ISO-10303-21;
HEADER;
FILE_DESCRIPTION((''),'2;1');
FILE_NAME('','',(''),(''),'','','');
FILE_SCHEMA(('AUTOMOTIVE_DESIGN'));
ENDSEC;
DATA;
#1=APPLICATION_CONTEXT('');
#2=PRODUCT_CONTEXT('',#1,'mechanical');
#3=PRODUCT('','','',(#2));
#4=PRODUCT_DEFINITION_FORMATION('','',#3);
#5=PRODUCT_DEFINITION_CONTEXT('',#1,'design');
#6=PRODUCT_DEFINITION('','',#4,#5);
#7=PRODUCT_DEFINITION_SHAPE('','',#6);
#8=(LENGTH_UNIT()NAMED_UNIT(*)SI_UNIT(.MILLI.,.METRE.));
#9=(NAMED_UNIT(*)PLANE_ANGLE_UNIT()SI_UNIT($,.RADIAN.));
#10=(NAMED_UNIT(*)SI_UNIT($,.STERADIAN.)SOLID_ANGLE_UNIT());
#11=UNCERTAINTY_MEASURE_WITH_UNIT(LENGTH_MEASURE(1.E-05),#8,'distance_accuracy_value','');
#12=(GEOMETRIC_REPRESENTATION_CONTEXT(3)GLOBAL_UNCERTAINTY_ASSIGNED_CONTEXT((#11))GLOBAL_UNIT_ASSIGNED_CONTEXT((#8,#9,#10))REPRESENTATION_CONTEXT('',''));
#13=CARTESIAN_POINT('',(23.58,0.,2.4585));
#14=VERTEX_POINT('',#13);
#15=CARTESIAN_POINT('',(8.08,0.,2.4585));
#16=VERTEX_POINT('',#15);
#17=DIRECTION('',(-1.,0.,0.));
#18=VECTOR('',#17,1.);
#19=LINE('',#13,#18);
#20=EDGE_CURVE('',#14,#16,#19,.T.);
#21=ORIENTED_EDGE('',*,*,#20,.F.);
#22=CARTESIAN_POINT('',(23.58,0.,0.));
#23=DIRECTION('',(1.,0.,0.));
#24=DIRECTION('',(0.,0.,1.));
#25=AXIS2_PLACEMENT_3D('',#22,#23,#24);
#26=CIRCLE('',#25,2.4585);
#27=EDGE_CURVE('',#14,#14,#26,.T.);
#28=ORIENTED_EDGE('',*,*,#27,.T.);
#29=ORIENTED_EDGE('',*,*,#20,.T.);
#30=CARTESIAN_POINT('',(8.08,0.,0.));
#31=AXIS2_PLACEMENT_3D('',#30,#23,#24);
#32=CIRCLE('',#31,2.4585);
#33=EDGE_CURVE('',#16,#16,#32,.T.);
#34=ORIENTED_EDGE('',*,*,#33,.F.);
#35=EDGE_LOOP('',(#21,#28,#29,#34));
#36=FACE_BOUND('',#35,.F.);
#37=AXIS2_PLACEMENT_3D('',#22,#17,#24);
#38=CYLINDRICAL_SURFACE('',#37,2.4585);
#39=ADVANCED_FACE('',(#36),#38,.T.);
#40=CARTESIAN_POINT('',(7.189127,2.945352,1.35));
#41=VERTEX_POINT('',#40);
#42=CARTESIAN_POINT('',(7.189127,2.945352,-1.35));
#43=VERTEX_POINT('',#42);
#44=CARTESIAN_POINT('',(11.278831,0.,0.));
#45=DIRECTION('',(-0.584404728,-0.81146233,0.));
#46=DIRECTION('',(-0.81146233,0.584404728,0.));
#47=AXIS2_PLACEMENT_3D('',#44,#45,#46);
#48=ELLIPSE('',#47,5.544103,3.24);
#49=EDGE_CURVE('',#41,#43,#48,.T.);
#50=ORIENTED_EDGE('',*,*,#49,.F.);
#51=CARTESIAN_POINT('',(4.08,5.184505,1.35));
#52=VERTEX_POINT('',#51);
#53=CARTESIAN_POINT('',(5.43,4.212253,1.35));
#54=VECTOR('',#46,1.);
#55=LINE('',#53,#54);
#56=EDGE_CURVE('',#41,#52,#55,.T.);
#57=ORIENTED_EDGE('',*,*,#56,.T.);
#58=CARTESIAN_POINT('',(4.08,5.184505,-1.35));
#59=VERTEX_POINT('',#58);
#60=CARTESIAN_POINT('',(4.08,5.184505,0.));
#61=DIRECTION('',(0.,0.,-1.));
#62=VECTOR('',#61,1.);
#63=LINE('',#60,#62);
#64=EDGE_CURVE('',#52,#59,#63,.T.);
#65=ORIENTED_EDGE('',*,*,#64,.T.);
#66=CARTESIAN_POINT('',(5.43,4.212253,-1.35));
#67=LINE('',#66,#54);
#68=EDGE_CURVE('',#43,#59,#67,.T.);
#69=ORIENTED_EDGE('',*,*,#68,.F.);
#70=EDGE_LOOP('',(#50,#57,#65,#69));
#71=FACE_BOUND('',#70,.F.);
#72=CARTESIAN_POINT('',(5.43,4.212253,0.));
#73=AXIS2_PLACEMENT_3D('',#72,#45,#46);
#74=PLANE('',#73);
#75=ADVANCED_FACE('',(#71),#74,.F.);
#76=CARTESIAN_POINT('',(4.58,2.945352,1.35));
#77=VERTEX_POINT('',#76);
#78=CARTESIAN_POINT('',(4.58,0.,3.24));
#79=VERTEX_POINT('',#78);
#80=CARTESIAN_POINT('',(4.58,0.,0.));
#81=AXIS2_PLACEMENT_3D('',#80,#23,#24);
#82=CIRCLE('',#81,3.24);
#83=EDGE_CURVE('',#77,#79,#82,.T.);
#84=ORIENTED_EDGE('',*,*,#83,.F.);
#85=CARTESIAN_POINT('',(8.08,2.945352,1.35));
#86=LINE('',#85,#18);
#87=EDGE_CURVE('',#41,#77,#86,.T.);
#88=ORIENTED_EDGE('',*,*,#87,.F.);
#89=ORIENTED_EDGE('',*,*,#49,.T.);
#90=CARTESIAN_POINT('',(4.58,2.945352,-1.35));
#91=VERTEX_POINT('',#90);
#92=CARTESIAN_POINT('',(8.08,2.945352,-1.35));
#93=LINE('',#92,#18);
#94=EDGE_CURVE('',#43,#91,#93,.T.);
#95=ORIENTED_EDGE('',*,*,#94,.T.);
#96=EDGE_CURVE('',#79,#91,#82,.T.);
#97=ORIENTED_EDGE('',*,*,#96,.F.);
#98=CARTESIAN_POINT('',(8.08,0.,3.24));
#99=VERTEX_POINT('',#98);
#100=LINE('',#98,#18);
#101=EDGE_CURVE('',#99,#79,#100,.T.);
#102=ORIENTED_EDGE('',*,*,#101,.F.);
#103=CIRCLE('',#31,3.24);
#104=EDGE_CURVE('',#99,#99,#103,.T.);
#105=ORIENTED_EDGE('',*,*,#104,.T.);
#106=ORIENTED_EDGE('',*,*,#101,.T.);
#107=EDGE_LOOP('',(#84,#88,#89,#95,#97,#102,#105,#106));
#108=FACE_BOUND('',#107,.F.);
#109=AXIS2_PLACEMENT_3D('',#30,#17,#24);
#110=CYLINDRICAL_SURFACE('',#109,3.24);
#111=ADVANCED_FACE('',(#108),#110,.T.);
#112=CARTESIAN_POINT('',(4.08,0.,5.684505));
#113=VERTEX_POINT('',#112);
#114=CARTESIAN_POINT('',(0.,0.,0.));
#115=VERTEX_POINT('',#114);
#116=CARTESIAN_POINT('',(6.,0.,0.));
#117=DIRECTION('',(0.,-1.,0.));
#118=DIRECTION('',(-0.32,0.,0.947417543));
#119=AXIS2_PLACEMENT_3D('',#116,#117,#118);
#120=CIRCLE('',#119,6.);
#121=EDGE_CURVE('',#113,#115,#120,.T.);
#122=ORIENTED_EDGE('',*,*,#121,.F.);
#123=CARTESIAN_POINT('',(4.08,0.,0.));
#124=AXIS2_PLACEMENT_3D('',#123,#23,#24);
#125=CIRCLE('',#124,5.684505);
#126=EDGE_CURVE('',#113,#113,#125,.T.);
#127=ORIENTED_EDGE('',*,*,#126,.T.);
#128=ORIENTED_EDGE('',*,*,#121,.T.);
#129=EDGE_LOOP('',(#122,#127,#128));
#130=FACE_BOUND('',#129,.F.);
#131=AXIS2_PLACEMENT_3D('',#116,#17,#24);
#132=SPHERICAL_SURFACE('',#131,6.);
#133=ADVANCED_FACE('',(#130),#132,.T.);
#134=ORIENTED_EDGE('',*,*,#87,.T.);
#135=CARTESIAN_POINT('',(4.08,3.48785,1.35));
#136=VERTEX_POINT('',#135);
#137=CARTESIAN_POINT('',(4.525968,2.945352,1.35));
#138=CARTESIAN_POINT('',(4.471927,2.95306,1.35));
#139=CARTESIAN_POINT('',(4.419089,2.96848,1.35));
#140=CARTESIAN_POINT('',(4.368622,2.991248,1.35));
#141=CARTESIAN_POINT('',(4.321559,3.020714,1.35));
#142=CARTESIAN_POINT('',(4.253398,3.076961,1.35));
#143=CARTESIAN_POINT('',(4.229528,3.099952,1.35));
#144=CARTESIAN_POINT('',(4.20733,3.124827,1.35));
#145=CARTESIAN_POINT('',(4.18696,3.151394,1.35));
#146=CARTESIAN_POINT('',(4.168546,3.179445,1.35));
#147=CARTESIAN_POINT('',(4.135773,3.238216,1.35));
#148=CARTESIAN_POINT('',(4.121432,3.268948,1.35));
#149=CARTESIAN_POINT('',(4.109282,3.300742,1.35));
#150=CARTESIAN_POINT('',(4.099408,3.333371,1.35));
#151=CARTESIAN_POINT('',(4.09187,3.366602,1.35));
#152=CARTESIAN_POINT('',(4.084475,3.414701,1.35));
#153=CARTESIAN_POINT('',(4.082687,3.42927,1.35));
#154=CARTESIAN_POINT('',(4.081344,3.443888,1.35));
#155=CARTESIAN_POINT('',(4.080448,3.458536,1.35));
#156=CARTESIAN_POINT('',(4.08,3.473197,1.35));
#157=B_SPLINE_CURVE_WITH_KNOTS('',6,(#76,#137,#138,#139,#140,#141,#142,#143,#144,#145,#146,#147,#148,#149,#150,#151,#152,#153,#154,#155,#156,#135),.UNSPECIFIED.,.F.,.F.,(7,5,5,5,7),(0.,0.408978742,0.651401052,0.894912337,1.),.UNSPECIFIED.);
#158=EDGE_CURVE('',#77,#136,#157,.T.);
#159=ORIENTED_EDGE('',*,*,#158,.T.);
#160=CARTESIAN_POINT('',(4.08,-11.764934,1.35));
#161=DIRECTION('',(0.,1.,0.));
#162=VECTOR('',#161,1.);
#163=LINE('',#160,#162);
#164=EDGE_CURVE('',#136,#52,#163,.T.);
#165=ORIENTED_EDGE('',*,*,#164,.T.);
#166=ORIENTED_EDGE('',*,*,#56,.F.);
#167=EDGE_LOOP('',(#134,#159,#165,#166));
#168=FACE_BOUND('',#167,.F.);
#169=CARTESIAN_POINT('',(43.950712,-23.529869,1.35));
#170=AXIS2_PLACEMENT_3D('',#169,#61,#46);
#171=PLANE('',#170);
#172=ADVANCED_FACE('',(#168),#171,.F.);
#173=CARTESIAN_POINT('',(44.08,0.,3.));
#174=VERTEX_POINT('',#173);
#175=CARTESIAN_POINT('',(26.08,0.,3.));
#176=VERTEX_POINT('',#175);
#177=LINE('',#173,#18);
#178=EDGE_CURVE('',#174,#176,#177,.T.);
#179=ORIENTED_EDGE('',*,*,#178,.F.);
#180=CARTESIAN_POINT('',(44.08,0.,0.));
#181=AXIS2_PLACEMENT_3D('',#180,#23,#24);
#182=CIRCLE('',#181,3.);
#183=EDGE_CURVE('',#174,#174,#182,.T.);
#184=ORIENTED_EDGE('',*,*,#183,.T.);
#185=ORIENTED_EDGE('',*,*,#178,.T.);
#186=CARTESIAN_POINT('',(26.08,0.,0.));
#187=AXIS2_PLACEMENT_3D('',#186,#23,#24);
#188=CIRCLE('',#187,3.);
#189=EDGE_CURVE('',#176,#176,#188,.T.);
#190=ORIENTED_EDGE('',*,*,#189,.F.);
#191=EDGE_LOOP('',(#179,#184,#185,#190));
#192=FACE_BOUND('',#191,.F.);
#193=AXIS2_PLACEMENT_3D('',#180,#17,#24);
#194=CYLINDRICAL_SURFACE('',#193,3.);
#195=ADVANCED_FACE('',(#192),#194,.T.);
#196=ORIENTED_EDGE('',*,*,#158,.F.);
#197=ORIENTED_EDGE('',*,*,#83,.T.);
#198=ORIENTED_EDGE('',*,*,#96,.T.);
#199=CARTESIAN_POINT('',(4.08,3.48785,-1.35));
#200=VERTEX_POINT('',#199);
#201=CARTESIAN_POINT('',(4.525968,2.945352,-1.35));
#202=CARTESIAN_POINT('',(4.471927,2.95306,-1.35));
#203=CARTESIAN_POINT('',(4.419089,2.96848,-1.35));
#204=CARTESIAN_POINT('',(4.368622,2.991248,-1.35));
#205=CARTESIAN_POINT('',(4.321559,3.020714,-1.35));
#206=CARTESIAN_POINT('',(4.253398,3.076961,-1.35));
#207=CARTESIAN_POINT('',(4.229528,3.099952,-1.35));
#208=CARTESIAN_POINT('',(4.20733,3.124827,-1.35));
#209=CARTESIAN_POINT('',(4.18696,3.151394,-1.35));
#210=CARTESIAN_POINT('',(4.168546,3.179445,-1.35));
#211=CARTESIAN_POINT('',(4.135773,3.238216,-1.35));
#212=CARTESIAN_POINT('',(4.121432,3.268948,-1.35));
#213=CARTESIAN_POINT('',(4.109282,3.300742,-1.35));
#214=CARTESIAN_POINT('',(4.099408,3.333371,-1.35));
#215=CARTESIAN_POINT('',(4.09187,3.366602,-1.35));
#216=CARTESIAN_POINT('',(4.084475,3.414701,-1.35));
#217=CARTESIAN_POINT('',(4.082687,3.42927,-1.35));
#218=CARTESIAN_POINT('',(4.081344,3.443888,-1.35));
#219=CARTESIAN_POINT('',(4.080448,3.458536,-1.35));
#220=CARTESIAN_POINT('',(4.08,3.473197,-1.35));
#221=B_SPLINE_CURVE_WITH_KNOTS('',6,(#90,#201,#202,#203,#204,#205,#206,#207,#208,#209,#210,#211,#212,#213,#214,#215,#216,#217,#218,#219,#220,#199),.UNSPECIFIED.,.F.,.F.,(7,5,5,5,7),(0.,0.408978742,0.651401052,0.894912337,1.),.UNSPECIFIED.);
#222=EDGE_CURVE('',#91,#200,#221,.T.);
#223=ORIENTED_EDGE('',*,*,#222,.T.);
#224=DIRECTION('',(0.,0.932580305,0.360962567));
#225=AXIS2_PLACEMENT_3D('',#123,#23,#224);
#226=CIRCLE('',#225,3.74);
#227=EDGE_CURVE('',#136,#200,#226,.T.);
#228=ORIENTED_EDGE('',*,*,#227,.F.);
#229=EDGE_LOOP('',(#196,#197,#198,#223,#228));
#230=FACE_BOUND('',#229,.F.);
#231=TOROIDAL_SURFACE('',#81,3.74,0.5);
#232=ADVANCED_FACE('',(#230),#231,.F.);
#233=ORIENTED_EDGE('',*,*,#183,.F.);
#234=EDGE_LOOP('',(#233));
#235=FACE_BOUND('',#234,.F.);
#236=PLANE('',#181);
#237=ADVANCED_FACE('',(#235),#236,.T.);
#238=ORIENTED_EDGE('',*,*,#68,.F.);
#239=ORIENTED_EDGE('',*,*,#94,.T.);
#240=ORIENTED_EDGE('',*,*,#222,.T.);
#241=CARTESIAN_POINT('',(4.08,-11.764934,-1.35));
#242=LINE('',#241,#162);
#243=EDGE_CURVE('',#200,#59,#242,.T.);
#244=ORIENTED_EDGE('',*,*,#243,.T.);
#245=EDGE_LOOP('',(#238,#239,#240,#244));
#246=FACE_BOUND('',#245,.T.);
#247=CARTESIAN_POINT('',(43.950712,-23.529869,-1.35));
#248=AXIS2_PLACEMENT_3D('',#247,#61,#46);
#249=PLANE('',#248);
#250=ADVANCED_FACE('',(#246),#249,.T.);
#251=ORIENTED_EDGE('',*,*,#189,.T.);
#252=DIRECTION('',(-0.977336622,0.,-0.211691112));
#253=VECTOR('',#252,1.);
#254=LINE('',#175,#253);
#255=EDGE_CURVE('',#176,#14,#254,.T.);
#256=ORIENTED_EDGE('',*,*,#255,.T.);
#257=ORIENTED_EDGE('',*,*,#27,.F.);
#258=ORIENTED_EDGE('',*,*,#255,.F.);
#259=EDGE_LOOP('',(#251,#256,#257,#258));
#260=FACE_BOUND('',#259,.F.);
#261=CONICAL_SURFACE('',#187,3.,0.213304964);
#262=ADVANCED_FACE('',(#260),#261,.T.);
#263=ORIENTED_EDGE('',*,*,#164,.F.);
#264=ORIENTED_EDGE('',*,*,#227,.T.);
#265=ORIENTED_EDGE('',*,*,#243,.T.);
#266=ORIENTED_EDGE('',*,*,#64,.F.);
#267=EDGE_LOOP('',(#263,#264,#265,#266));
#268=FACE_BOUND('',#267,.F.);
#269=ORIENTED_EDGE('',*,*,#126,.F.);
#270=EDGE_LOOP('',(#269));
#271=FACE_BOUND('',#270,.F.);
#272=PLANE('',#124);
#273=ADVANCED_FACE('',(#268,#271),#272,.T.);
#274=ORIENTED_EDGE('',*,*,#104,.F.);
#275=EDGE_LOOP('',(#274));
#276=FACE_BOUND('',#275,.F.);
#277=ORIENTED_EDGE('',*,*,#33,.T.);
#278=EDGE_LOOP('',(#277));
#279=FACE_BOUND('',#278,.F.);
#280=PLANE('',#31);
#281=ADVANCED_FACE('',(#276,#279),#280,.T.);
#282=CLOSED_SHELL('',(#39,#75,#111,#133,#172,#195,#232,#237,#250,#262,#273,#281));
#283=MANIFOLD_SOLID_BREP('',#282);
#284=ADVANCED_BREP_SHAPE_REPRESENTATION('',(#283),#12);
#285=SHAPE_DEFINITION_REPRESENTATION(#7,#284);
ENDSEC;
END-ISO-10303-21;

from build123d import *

# Parameters (mm, degrees)
NIB_REACH      = 46.807
SKETCH2_WALL_W = 94.941468098
SKETCH2_WALL_H = 2.7


with BuildPart() as part:
    # Sketch1 → Base (revolve)
    with BuildSketch(Plane.XY, mode=Mode.PRIVATE) as base_sk:
        with BuildLine():
            Line((44.08, 0), (44.08, 3))
            Line((44.08, 3), (8.08, 3))
            Line((8.08, 3), (8.08, 3.24))
            Line((8.08, 3.24), (4.58, 3.24))
            ThreePointArc((4.58, 3.24), (4.226446609, 3.386446609), (4.08, 3.74))
            Line((4.08, 3.74), (4.08, 5.684505256))
            ThreePointArc((4.08, 5.684505256), (1.125576957, 3.498571137), (0, 0))
            Line((0, 0), (44.08, 0))
        make_face()
    revolve(base_sk.sketch.rotate(Axis((-31.484345479, 0, 0), (1, 0, 0)), 90), axis=Axis((-31.484345479, 0, 0), (1, 0, 0)))

    # Sketch2 wall → Nib (add, up to next)
    with BuildSketch(Plane(origin=(5.43, 4.212252628, 0), x_dir=(-0.811462330335, 0.58440472829, 0), z_dir=(-0.58440472829, -0.811462330335, 0)), mode=Mode.PRIVATE) as nib_sk1:
        Rectangle(SKETCH2_WALL_W, SKETCH2_WALL_H)
    nib_tool1 = extrude(nib_sk1.sketch, amount=NIB_REACH, mode=Mode.PRIVATE) - part.part
    add(nib_tool1.solids().sort_by_distance((5.43, 4.212252628, 0))[0])

    # Sketch3 → Cut-Revolve1 (revolve, cut)
    with BuildSketch(Plane.XY, mode=Mode.PRIVATE) as cut_revolve1_sk:
        Polygon((26.08, 3), (23.58, 2.4585), (8.08, 2.4585), (8.08, 3), align=None)
    revolve(cut_revolve1_sk.sketch.rotate(Axis((-29.816341648, 0, 0), (1, 0, 0)), 90), axis=Axis((-29.816341648, 0, 0), (1, 0, 0)), mode=Mode.SUBTRACT)


solid = part.part
